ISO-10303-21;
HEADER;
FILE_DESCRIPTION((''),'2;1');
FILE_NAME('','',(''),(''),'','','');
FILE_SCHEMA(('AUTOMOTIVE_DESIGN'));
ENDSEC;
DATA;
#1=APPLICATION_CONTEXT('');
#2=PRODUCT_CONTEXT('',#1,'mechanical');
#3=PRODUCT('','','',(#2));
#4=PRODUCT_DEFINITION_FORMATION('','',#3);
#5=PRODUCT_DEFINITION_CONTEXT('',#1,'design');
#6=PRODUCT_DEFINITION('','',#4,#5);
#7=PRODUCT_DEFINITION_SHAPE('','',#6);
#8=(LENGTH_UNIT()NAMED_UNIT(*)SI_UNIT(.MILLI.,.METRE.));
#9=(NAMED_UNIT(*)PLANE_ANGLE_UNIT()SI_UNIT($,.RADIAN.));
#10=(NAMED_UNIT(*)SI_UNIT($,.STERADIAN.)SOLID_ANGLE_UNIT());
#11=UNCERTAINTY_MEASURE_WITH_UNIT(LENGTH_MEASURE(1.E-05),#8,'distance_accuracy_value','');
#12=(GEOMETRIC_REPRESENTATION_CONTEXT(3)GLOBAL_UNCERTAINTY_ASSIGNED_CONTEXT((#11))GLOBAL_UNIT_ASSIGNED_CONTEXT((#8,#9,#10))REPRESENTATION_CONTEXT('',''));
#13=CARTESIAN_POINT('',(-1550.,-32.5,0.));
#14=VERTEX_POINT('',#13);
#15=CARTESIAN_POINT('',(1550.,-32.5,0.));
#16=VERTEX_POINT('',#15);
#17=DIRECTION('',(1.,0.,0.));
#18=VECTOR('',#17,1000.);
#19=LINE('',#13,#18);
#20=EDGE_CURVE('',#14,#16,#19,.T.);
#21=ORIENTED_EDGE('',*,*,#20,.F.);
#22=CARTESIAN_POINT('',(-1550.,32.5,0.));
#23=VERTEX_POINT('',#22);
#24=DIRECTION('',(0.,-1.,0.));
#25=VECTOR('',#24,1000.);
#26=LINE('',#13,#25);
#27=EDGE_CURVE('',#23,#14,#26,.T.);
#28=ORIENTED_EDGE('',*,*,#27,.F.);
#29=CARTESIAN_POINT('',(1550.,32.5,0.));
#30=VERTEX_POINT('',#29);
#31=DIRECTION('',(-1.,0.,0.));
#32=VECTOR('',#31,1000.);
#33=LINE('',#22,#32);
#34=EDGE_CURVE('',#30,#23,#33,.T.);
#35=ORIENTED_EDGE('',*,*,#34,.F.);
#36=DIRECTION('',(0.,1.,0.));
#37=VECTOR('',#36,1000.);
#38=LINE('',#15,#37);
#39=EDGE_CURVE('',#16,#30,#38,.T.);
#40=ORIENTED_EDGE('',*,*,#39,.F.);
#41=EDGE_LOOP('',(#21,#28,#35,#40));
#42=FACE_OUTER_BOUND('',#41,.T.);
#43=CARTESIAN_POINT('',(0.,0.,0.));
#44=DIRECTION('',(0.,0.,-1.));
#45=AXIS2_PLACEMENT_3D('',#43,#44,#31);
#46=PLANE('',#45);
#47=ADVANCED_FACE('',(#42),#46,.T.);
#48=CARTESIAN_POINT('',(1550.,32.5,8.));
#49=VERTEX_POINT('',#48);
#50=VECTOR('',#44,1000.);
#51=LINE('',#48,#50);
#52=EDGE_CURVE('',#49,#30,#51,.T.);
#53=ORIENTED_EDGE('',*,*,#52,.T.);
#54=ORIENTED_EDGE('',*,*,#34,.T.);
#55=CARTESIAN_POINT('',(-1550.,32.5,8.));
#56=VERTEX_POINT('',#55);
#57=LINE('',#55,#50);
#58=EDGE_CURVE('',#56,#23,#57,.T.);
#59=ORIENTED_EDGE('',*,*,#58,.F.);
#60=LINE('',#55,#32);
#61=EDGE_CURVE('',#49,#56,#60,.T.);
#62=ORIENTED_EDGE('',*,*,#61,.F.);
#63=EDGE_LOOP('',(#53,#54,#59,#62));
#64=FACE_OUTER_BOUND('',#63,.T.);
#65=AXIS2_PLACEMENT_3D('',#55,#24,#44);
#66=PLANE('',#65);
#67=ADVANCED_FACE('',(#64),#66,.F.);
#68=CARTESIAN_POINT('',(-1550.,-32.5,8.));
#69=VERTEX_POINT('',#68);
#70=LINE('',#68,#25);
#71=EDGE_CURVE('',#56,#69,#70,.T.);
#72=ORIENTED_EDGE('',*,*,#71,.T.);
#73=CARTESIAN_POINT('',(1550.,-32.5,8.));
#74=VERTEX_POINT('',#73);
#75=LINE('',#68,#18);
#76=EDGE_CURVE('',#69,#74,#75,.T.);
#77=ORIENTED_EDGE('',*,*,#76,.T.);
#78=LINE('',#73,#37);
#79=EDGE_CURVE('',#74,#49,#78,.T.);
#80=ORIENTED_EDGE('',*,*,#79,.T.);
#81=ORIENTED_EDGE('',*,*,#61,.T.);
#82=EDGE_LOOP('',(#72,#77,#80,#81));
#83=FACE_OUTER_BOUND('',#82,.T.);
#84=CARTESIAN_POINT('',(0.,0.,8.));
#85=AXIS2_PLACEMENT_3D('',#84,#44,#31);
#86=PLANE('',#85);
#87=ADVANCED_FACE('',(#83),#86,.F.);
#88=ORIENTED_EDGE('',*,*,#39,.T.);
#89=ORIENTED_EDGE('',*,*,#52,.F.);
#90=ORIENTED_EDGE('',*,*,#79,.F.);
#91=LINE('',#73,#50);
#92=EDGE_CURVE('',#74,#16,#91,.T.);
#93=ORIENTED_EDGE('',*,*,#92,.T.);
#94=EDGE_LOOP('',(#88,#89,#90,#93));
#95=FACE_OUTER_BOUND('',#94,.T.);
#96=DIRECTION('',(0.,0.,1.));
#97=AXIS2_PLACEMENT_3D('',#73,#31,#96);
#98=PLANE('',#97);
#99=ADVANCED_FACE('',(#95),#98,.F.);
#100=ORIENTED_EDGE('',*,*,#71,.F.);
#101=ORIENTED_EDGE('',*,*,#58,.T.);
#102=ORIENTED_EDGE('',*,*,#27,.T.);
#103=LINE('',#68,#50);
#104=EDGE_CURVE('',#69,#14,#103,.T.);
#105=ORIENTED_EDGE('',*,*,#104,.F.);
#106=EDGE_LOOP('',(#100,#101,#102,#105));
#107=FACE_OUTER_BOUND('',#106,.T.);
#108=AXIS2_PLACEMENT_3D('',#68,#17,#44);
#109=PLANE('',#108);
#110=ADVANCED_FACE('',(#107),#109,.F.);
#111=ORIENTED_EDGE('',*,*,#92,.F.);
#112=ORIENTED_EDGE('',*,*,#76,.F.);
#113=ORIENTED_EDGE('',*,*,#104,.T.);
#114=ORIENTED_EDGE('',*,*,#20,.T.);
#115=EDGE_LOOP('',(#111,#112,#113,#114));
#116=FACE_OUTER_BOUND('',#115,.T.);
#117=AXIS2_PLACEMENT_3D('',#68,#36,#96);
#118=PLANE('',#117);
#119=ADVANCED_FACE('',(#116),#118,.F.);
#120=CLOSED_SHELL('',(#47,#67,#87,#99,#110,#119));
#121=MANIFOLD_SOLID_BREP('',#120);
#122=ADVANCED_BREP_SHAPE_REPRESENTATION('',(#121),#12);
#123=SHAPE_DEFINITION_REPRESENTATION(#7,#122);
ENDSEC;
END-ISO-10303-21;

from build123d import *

# Parameters (mm, degrees)
SKETCH1_W           = 3100
SKETCH1_H           = 65
BOSS_EXTRUDE1_DEPTH = 8


with BuildPart() as part:
    # Sketch1 → Boss-Extrude1 (new body)
    with BuildSketch(Plane.XY):
        Rectangle(SKETCH1_W, SKETCH1_H)
    extrude(amount=BOSS_EXTRUDE1_DEPTH)


solid = part.part
